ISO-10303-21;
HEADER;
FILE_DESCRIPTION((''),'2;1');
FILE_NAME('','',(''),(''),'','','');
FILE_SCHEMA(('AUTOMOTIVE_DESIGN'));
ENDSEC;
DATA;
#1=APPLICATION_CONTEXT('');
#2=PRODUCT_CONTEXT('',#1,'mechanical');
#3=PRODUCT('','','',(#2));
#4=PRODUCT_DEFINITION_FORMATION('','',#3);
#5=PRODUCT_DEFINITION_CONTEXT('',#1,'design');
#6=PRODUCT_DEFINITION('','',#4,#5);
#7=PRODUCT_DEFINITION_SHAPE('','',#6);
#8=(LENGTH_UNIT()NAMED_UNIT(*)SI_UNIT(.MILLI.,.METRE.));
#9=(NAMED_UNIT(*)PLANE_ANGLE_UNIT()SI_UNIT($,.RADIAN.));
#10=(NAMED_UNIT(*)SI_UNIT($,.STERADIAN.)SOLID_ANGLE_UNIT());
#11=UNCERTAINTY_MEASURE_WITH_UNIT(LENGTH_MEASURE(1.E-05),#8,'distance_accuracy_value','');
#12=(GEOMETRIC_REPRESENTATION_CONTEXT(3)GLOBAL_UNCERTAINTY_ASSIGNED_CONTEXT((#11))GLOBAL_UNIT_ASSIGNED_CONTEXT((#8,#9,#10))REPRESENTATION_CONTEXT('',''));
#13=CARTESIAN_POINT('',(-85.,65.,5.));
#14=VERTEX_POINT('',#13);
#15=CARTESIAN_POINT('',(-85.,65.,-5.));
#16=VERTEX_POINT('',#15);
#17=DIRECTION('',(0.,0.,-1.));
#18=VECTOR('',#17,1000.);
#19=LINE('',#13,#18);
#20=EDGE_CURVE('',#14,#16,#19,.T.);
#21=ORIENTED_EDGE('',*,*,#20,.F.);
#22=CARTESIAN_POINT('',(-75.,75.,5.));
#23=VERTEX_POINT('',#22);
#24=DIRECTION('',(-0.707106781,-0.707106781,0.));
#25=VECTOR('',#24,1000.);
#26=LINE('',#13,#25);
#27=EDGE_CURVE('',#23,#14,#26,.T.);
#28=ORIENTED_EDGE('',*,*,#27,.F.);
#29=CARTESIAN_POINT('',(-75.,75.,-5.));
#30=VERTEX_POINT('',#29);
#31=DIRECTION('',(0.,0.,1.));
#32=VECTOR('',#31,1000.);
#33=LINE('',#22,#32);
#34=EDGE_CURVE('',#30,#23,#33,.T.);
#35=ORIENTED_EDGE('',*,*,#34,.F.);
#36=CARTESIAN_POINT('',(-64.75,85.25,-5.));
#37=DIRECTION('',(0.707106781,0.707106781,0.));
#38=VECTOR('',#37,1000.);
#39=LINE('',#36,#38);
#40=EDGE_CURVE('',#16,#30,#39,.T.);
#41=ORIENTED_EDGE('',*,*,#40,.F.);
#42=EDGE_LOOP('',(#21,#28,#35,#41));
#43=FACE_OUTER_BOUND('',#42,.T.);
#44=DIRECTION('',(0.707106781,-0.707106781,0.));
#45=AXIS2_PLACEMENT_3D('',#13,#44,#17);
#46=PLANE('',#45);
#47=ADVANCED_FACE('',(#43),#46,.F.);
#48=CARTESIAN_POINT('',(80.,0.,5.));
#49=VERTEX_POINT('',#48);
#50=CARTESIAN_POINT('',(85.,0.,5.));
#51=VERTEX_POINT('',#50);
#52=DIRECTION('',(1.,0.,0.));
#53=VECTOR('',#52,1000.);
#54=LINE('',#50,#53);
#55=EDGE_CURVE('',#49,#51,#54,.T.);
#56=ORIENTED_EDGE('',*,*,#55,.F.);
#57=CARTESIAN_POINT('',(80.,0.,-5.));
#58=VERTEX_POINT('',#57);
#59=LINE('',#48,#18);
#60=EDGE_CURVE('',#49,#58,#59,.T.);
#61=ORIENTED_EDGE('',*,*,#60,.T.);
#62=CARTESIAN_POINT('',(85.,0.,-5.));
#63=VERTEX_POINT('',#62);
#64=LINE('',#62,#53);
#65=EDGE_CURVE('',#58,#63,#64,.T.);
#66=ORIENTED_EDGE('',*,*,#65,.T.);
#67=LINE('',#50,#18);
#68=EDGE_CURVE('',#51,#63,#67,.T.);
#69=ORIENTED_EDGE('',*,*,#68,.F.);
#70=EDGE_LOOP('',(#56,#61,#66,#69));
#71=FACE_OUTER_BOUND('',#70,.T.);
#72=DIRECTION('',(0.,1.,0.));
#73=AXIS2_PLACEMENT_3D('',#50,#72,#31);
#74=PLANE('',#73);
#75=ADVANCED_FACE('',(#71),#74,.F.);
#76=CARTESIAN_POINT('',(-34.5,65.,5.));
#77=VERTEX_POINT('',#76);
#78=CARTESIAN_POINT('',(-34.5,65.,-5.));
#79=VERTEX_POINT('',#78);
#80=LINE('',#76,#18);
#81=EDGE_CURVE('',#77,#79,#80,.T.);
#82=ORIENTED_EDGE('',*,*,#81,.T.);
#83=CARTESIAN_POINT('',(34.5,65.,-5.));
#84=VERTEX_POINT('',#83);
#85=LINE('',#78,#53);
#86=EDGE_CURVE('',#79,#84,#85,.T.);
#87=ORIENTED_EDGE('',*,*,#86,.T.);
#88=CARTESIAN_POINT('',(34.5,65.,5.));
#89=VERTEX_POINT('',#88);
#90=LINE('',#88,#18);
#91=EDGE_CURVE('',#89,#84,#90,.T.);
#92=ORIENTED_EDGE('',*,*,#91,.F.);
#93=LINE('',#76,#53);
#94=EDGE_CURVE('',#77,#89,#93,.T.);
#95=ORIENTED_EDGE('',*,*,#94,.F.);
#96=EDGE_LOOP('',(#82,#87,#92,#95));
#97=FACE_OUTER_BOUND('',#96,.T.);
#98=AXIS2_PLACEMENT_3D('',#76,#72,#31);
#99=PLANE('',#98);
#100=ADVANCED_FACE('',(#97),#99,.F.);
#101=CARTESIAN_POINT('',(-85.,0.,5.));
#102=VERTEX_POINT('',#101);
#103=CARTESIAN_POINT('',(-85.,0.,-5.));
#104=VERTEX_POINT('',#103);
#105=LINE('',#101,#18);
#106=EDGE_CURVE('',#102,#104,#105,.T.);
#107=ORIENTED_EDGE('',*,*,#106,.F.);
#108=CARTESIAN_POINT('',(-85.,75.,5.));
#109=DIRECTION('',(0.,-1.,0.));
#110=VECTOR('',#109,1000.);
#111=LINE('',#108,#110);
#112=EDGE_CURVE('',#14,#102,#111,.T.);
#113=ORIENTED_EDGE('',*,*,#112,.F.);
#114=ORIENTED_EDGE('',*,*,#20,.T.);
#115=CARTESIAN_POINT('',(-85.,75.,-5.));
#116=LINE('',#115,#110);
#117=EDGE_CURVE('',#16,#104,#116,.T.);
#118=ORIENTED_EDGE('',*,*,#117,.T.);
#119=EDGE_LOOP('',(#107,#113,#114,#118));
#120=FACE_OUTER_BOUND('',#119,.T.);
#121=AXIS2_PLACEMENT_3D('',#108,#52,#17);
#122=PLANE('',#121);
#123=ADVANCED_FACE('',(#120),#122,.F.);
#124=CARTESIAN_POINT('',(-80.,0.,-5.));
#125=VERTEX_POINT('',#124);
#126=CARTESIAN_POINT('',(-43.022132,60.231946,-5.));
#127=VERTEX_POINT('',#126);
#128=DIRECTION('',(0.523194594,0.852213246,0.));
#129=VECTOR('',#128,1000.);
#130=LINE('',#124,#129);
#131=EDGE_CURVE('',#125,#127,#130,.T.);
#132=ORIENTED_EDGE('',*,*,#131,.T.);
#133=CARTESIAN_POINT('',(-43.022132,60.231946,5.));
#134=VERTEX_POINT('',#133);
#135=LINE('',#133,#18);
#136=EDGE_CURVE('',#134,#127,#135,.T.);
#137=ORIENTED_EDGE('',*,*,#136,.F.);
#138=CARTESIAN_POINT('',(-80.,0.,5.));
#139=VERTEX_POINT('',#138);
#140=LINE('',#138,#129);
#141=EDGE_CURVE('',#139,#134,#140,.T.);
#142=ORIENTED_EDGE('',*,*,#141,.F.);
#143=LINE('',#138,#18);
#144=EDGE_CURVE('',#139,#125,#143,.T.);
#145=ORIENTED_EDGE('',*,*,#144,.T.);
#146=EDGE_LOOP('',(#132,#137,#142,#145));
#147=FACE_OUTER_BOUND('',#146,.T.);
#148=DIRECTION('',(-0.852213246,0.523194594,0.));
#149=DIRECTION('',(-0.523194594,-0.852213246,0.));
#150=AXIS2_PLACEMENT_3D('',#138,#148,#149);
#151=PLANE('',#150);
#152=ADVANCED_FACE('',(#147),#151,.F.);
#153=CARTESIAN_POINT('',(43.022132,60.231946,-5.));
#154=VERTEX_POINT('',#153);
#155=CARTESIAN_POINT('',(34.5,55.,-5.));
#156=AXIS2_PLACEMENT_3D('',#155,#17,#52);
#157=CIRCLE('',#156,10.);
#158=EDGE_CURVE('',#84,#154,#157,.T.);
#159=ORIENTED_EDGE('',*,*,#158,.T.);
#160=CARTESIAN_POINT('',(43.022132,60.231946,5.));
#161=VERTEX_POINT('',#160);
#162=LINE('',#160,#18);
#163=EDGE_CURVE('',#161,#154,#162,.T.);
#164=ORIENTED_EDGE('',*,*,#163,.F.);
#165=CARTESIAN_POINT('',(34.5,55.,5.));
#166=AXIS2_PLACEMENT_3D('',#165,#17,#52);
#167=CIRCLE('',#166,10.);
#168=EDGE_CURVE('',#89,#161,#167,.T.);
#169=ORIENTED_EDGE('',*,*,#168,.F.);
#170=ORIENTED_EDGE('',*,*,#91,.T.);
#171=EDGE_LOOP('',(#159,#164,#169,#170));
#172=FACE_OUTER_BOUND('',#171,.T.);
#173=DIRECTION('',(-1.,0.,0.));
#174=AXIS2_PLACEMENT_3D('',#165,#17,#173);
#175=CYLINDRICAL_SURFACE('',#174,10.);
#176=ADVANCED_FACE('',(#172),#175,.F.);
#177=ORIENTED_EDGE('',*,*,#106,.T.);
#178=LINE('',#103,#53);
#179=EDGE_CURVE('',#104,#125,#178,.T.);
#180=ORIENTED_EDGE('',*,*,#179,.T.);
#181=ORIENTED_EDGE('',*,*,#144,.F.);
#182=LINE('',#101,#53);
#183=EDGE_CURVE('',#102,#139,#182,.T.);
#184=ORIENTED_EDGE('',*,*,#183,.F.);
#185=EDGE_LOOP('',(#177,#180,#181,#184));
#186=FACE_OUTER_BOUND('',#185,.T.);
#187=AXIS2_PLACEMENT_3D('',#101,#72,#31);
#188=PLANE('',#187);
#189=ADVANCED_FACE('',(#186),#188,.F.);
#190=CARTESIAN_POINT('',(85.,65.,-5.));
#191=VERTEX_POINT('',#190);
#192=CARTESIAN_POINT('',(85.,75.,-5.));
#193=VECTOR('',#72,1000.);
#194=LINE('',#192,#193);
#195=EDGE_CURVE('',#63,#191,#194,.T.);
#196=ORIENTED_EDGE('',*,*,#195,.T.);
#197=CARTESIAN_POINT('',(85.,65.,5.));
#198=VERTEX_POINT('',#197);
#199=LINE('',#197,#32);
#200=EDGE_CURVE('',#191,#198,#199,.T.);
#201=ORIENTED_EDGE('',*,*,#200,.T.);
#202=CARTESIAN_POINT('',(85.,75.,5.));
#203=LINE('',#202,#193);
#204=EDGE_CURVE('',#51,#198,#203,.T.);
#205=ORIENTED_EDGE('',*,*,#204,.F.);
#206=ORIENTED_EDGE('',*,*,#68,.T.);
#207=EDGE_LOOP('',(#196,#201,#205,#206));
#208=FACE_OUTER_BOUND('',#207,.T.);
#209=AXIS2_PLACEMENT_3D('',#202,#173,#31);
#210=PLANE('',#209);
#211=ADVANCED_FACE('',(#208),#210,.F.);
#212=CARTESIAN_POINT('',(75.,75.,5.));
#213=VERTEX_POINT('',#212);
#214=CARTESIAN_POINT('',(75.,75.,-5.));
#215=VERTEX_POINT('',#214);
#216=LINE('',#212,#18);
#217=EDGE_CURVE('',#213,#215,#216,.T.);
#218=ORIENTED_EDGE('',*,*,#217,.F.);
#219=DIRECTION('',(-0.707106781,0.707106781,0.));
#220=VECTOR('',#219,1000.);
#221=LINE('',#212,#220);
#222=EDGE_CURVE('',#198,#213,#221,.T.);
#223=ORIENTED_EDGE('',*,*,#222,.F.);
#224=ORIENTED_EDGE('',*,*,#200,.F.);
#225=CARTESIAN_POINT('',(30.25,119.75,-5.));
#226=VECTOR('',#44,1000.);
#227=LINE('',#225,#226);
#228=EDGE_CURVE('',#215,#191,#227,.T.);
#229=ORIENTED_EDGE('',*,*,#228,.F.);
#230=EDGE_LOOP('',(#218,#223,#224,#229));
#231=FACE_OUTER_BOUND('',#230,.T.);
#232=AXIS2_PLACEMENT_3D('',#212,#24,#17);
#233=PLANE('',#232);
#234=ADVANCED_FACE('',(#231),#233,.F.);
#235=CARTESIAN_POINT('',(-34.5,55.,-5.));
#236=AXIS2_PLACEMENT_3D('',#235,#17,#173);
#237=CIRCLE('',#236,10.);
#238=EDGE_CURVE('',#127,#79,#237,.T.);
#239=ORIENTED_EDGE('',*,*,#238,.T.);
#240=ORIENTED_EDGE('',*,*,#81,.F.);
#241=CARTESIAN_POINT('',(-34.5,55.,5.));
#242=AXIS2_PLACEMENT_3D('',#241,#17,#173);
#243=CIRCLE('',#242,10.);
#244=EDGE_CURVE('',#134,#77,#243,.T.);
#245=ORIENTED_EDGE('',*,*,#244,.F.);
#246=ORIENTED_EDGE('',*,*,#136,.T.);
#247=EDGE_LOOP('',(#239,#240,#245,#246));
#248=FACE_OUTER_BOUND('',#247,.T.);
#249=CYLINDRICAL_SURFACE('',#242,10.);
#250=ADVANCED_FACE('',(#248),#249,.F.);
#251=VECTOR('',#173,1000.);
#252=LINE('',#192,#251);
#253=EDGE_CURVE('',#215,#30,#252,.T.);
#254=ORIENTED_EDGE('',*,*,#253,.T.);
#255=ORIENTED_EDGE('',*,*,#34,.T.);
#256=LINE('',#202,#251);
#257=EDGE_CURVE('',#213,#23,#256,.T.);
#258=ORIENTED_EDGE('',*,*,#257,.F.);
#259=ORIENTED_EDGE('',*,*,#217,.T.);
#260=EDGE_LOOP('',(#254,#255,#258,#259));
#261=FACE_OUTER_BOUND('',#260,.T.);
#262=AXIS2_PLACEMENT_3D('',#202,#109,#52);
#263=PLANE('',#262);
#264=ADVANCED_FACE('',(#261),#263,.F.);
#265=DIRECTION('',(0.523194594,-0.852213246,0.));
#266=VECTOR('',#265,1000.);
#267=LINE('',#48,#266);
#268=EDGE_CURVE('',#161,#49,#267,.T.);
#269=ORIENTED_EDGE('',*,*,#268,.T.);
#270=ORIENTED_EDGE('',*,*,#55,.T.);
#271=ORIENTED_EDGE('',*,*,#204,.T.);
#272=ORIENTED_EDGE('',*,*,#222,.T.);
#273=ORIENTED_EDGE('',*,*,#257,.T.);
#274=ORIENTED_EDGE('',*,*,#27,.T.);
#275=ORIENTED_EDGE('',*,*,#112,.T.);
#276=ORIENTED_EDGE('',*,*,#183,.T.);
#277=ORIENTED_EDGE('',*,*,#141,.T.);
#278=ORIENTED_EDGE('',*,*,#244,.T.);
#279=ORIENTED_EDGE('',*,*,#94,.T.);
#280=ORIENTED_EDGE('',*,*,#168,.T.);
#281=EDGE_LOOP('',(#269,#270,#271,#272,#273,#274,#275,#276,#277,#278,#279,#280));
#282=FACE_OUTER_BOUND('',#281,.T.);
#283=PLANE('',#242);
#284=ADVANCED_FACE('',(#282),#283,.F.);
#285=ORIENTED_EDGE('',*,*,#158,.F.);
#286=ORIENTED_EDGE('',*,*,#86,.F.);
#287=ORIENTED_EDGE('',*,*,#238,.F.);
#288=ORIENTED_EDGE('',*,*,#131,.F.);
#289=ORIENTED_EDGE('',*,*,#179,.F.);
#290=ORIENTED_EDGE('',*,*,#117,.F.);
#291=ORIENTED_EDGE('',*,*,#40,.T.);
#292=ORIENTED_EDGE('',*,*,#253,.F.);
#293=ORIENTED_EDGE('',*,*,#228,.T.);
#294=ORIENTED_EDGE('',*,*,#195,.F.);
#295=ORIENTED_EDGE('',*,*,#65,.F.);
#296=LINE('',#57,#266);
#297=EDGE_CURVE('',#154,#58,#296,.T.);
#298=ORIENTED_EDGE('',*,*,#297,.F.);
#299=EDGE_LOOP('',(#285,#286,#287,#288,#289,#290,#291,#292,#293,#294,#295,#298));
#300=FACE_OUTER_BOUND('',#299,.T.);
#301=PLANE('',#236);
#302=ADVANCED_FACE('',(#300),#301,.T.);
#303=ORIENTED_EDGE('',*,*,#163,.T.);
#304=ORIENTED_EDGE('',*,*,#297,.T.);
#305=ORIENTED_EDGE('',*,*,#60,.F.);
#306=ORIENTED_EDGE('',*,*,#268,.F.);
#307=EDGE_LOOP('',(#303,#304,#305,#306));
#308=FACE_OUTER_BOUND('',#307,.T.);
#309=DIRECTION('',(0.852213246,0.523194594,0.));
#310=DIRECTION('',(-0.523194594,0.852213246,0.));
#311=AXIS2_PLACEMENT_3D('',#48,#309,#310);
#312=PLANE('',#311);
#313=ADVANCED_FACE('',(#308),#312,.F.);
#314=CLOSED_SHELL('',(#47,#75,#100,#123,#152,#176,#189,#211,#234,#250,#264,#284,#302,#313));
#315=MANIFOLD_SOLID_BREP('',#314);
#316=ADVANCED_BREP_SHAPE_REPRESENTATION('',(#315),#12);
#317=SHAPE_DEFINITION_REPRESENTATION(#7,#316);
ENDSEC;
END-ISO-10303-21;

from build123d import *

# Parameters (mm, degrees)
BOSS_EXTRUDE1_DEPTH = 5
CHAMFER1_SIZE       = 10


with BuildPart() as part:
    # Sketch1 → Boss-Extrude1 (new, symmetric)
    with BuildSketch(Plane.XY):
        with BuildLine():
            Line((-85, 0), (-80, 0))
            Line((-80, 0), (-43.022132459, 60.231945943))
            ThreePointArc((-43.022132459, 60.231945943), (-39.382649924, 63.726954206), (-34.5, 65))
            Line((-34.5, 65), (34.5, 65))
            ThreePointArc((34.5, 65), (39.382649924, 63.726954206), (43.022132459, 60.231945943))
            Line((43.022132459, 60.231945943), (80, 0))
            Line((80, 0), (85, 0))
            Line((85, 0), (85, 75))
            Line((85, 75), (-85, 75))
            Line((-85, 75), (-85, 0))
        make_face()
    extrude(amount=BOSS_EXTRUDE1_DEPTH, both=True)

    # Chamfer1
    chamfer1_edges = [part.edges().sort_by_distance(p)[0] for p in [
        (-85, 75, 0),
        (85, 75, 0),
    ]]
    chamfer(chamfer1_edges, length=CHAMFER1_SIZE)


solid = part.part
